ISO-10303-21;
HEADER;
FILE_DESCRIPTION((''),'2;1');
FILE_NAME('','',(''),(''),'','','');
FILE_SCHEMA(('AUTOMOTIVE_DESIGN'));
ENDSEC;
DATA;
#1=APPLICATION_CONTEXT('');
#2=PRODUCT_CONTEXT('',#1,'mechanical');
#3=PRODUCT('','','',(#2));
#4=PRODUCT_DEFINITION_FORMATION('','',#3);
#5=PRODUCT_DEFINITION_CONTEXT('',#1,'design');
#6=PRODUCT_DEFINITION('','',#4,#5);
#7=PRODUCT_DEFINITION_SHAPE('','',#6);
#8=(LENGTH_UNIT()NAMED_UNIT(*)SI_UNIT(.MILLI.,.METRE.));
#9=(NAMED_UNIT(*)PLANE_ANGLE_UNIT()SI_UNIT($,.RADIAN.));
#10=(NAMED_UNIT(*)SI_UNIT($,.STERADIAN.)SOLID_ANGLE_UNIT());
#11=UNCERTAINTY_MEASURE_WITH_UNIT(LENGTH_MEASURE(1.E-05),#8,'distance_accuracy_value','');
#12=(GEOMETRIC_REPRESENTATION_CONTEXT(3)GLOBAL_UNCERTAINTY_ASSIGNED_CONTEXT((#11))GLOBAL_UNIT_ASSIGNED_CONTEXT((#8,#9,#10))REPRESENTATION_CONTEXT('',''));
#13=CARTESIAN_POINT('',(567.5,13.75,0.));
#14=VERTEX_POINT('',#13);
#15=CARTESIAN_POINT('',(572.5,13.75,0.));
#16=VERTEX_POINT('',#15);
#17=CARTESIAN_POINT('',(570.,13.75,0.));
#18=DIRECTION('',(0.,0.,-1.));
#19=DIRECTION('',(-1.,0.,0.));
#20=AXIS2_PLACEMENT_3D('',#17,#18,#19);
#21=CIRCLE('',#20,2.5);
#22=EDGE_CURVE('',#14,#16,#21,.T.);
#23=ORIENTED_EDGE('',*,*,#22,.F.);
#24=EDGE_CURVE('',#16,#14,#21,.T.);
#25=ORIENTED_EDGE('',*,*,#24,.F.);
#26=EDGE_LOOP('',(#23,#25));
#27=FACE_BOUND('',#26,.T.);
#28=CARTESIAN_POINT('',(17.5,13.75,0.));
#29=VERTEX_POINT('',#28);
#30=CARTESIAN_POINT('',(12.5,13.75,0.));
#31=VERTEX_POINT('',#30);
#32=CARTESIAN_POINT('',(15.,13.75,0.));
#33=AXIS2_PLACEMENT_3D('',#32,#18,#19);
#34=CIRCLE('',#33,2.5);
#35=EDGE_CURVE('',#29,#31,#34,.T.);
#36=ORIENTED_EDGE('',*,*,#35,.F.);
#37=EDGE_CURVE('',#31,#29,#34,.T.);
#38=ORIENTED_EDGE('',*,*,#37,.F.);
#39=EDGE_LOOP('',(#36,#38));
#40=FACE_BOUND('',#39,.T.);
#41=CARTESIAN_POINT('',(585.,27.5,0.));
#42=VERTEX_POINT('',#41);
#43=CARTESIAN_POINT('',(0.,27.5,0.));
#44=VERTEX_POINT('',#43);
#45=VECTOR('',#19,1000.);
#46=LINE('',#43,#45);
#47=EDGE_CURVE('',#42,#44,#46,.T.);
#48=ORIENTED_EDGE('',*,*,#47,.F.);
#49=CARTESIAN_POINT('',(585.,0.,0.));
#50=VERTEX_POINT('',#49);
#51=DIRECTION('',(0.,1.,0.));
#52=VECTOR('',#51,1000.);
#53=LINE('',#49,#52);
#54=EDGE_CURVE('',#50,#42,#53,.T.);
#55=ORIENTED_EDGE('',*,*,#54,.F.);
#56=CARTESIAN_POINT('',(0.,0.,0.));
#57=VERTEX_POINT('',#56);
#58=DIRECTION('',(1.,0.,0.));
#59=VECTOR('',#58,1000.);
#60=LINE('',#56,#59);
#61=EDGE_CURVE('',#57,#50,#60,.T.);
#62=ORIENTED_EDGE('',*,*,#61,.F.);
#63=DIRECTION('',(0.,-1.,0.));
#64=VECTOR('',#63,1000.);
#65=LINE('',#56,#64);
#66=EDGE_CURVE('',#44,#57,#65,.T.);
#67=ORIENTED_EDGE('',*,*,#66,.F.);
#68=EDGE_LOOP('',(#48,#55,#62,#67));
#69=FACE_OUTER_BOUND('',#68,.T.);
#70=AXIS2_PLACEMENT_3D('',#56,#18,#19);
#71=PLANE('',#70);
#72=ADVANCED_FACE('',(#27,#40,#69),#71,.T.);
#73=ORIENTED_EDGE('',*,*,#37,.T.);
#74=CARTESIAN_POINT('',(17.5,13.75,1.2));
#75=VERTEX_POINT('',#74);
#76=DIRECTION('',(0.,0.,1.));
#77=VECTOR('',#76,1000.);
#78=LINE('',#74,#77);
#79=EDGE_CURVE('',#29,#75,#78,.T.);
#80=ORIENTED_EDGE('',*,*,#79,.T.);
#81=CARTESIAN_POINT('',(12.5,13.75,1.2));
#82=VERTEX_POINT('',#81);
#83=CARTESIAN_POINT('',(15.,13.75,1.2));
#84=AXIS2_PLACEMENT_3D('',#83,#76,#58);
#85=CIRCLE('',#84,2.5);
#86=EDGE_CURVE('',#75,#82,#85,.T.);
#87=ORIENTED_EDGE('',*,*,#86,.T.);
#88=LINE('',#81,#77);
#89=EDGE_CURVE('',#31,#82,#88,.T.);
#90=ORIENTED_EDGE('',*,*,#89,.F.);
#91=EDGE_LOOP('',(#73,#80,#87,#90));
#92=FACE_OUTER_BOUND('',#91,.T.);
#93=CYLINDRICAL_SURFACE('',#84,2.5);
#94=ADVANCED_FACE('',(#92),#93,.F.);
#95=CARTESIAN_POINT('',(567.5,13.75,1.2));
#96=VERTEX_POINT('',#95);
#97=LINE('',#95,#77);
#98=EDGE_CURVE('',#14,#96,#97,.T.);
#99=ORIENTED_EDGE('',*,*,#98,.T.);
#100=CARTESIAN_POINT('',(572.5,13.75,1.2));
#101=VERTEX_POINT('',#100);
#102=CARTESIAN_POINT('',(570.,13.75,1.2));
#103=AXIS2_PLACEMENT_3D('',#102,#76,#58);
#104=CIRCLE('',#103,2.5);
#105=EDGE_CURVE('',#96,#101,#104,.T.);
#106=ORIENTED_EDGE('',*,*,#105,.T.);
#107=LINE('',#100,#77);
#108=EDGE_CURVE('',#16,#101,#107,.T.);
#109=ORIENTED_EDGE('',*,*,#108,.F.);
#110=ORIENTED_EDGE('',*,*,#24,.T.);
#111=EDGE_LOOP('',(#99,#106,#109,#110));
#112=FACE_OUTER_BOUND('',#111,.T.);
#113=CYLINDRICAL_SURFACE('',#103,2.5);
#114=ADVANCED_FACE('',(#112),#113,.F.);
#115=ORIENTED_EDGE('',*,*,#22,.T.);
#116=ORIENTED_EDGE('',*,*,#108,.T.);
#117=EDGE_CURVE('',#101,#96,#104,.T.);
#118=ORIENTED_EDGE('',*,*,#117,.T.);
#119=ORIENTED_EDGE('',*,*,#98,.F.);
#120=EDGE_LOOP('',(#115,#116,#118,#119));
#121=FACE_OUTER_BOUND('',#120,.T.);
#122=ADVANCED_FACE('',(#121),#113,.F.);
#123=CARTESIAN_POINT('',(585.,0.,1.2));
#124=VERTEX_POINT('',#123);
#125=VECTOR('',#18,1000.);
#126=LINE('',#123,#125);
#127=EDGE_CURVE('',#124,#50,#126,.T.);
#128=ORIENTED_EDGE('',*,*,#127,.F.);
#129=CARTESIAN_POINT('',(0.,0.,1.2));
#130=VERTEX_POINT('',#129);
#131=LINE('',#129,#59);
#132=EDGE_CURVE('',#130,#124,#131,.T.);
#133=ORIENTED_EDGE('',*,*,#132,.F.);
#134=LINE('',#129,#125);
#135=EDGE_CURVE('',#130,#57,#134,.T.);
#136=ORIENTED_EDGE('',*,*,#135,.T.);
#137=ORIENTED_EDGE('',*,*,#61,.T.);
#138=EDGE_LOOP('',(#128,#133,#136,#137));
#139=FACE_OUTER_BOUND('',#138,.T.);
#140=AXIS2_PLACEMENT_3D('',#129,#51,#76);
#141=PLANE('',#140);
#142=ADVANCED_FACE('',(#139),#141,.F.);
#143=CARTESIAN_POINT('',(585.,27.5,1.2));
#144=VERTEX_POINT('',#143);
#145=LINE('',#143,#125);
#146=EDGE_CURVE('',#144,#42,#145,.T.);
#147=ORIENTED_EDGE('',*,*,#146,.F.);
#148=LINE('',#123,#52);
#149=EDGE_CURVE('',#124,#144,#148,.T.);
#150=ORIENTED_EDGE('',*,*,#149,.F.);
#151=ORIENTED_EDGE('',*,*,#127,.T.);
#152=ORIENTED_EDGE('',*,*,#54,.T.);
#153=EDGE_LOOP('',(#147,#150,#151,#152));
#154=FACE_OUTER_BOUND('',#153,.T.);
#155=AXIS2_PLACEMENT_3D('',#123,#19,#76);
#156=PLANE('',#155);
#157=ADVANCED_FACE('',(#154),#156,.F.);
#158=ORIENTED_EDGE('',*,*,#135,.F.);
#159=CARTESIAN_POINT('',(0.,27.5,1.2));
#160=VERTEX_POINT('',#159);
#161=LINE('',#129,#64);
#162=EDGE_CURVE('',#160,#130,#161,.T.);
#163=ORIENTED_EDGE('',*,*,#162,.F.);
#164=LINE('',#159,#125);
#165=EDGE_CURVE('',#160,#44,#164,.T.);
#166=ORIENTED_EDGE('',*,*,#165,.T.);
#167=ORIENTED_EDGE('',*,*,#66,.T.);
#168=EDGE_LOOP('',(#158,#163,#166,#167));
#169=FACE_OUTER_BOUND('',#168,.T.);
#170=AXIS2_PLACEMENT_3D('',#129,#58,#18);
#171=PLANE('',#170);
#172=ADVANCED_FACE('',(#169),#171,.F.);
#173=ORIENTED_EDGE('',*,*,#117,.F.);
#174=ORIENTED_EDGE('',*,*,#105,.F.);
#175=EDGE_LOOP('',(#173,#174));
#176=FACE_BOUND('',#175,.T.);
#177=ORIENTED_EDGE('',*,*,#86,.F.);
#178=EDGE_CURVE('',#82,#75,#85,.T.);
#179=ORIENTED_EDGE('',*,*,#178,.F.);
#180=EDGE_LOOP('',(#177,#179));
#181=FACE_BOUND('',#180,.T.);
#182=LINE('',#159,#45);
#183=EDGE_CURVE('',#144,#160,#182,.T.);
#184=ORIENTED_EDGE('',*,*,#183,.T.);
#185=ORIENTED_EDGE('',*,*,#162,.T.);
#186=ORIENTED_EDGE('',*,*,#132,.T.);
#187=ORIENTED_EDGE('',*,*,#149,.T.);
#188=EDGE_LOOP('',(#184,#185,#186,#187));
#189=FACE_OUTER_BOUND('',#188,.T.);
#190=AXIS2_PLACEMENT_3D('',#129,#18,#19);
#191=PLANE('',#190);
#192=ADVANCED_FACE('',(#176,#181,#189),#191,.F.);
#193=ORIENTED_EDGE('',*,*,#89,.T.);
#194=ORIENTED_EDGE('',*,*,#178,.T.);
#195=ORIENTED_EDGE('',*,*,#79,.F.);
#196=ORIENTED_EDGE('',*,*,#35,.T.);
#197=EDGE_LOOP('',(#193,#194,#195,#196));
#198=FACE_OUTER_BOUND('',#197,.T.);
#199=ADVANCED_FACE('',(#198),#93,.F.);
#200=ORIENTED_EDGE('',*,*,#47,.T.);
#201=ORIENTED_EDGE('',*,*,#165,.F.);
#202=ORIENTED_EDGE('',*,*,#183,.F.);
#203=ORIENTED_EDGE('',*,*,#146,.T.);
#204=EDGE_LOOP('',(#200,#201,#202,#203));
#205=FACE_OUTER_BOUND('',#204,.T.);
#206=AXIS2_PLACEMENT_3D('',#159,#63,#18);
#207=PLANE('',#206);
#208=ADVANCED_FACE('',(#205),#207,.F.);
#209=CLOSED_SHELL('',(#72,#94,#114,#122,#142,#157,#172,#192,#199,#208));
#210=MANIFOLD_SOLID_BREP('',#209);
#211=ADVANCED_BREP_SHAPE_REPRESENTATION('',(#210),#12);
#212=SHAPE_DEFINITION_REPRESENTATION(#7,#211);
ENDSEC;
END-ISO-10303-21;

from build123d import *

# Parameters (mm, degrees)
SKETCH_1_W                = 585
SKETCH_1_H                = 27.5
EXTRUDE_1_DEPTH           = 1.2
HOLE_WIZARD_5_0_5_1_D     = 5
HOLE_WIZARD_5_0_5_1_DEPTH = 5
HOLE_WIZARD_5_0_5_1_TIP   = 1.502151548


with BuildPart() as part:
    # 草图1 → 凸台-拉伸1 (new body)
    with BuildSketch(Plane.XY):
        with Locations((292.5, 13.75)):
            Rectangle(SKETCH_1_W, SKETCH_1_H)
    extrude(amount=EXTRUDE_1_DEPTH)

    # Ø5.0 (5) 直径孔1
    with Locations(Plane.XY.offset(1.2)):
        with Locations((15, 13.75), (570, 13.75)):
            Hole(HOLE_WIZARD_5_0_5_1_D / 2, depth=HOLE_WIZARD_5_0_5_1_DEPTH)
            with Locations((0, 0, -(HOLE_WIZARD_5_0_5_1_DEPTH + HOLE_WIZARD_5_0_5_1_TIP / 2))):  # 118° drill point
                Cone(0, HOLE_WIZARD_5_0_5_1_D / 2, HOLE_WIZARD_5_0_5_1_TIP, mode=Mode.SUBTRACT)


solid = part.part
